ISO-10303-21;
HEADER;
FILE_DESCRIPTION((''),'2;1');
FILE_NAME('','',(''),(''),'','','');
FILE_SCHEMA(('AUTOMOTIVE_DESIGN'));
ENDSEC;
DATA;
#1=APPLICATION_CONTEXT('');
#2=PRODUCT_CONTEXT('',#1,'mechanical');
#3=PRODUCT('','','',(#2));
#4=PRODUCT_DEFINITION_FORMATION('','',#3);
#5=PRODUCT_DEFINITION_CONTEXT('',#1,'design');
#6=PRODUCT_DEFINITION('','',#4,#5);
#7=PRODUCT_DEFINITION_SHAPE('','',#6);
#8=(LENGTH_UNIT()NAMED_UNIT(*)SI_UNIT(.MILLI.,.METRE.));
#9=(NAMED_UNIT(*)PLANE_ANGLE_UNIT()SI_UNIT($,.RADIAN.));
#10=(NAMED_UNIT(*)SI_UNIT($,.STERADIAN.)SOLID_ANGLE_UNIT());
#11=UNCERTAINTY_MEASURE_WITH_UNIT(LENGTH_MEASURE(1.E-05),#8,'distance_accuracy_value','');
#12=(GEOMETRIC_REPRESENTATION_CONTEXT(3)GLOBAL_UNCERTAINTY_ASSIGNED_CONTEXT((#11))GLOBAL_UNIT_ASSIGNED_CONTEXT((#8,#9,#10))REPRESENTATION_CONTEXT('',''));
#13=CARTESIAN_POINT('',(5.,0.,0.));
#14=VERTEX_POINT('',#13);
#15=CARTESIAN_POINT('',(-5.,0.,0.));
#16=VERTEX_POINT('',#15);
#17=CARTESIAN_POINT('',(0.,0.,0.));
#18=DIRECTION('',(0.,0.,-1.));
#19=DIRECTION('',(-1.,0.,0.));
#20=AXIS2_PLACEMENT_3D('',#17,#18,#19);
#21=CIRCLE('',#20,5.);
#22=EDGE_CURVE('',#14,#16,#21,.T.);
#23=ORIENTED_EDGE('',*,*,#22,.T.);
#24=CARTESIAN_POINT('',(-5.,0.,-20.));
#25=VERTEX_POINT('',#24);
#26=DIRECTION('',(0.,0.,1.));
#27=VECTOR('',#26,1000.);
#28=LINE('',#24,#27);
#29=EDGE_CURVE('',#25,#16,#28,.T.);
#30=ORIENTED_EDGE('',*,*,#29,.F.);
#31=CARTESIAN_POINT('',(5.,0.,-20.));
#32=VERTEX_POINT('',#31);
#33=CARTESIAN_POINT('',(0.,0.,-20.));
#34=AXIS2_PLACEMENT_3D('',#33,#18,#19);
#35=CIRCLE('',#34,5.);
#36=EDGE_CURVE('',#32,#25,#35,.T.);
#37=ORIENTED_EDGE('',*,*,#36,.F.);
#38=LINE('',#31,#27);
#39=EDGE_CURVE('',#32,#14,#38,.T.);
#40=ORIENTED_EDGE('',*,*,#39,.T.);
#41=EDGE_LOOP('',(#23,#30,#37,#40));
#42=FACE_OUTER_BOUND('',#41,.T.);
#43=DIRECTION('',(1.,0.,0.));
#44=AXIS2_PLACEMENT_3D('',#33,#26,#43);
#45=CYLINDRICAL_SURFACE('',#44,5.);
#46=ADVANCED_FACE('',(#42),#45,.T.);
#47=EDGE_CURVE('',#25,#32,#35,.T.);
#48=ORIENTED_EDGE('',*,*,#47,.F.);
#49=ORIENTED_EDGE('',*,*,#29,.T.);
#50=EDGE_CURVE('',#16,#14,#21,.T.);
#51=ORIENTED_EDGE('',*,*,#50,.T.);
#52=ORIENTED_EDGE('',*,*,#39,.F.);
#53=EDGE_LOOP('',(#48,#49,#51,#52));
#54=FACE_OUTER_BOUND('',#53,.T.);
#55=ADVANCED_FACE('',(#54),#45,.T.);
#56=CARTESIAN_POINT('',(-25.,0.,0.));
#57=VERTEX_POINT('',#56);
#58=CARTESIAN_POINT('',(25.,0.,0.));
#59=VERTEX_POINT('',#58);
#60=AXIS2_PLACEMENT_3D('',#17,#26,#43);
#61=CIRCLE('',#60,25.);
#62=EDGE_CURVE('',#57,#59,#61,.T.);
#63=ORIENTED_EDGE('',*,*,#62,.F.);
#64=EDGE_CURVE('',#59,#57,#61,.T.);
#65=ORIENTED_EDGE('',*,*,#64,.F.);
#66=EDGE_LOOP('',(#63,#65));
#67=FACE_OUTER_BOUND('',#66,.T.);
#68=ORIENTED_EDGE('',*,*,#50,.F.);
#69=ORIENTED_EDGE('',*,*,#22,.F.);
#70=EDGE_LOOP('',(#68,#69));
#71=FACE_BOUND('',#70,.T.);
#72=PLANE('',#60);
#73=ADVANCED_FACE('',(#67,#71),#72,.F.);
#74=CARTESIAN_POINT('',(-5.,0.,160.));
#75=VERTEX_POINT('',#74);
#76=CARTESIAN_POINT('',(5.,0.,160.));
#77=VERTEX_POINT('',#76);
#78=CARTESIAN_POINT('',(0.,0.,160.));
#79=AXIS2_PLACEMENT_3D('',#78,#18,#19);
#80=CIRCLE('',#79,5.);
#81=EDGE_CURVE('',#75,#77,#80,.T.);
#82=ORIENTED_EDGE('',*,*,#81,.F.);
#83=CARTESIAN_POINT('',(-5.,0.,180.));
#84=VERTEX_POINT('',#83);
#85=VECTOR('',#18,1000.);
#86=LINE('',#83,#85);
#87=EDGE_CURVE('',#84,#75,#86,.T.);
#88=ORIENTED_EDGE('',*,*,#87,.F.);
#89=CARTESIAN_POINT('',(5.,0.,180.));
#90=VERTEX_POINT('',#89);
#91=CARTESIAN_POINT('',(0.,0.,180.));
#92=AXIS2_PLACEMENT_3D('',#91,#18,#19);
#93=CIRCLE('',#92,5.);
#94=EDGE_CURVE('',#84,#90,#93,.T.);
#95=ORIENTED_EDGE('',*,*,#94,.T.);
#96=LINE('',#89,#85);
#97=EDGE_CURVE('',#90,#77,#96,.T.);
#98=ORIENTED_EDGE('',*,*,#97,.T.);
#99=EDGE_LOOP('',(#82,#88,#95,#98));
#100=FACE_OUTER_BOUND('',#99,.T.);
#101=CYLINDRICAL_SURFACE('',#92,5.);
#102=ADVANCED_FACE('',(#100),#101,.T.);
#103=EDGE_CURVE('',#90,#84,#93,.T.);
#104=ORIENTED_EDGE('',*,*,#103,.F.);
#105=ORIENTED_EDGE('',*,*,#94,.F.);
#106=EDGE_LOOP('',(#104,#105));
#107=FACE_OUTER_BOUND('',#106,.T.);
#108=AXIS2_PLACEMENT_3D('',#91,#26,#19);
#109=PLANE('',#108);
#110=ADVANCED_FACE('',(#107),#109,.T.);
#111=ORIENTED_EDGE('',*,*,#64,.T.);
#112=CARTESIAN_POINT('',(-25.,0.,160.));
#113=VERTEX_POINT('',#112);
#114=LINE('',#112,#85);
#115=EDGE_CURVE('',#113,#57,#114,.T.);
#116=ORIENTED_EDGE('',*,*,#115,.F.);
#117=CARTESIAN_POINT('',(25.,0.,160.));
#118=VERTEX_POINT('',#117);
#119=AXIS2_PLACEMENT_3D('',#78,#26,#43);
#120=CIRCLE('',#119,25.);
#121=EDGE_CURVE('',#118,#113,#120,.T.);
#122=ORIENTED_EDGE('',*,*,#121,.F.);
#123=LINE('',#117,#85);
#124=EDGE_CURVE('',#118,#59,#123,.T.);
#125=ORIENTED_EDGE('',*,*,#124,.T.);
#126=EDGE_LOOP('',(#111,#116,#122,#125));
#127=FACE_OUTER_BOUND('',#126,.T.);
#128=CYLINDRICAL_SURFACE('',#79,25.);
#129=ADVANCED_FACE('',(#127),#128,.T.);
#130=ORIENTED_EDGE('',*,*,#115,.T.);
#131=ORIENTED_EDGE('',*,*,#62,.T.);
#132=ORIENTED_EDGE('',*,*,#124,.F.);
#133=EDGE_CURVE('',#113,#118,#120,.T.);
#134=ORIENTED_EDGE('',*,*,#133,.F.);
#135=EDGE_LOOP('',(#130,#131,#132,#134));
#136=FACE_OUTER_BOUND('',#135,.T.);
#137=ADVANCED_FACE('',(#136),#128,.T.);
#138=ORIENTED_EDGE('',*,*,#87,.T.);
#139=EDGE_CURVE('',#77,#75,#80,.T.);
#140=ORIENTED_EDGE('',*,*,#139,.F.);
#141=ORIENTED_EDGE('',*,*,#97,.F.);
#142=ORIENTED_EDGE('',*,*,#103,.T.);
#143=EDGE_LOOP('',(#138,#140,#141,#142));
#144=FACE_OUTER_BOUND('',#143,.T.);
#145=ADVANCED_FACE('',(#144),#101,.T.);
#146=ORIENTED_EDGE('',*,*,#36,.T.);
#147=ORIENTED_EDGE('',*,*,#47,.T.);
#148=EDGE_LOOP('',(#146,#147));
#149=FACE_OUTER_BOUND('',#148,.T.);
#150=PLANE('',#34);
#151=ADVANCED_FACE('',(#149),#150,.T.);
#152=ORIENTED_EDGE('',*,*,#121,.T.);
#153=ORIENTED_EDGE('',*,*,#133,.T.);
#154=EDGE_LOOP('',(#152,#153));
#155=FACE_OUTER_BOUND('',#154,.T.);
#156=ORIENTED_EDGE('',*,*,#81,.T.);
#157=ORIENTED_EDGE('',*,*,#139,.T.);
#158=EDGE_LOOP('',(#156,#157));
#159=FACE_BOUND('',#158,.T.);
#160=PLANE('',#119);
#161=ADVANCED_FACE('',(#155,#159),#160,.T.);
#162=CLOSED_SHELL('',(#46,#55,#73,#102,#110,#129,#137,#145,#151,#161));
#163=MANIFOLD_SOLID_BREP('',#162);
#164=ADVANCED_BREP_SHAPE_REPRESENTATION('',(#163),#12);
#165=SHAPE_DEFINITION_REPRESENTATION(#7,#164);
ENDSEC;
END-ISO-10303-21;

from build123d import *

# Parameters (mm, degrees)
SKETCH1_R           = 25
BOSS_EXTRUDE1_DEPTH = 160
SKETCH2_R           = 5
BOSS_EXTRUDE2_DEPTH = 20


with BuildPart() as part:
    # Sketch1 → Boss-Extrude1 (new body)
    with BuildSketch(Plane.XY):
        Circle(SKETCH1_R)
    extrude(amount=BOSS_EXTRUDE1_DEPTH)

    # Sketch2 → Boss-Extrude2 (add)
    with BuildSketch(Plane(origin=(0, 0, 0), x_dir=(-1, 0, 0), z_dir=(0, 0, -1))):
        Circle(SKETCH2_R)
    boss_extrude2 = extrude(amount=BOSS_EXTRUDE2_DEPTH)

    # Mirror1: Boss-Extrude2 across plane
    add(boss_extrude2.mirror(Plane(origin=(0, 0, 80), x_dir=(1, 0, 0), z_dir=(0, 0, -1))))


solid = part.part
